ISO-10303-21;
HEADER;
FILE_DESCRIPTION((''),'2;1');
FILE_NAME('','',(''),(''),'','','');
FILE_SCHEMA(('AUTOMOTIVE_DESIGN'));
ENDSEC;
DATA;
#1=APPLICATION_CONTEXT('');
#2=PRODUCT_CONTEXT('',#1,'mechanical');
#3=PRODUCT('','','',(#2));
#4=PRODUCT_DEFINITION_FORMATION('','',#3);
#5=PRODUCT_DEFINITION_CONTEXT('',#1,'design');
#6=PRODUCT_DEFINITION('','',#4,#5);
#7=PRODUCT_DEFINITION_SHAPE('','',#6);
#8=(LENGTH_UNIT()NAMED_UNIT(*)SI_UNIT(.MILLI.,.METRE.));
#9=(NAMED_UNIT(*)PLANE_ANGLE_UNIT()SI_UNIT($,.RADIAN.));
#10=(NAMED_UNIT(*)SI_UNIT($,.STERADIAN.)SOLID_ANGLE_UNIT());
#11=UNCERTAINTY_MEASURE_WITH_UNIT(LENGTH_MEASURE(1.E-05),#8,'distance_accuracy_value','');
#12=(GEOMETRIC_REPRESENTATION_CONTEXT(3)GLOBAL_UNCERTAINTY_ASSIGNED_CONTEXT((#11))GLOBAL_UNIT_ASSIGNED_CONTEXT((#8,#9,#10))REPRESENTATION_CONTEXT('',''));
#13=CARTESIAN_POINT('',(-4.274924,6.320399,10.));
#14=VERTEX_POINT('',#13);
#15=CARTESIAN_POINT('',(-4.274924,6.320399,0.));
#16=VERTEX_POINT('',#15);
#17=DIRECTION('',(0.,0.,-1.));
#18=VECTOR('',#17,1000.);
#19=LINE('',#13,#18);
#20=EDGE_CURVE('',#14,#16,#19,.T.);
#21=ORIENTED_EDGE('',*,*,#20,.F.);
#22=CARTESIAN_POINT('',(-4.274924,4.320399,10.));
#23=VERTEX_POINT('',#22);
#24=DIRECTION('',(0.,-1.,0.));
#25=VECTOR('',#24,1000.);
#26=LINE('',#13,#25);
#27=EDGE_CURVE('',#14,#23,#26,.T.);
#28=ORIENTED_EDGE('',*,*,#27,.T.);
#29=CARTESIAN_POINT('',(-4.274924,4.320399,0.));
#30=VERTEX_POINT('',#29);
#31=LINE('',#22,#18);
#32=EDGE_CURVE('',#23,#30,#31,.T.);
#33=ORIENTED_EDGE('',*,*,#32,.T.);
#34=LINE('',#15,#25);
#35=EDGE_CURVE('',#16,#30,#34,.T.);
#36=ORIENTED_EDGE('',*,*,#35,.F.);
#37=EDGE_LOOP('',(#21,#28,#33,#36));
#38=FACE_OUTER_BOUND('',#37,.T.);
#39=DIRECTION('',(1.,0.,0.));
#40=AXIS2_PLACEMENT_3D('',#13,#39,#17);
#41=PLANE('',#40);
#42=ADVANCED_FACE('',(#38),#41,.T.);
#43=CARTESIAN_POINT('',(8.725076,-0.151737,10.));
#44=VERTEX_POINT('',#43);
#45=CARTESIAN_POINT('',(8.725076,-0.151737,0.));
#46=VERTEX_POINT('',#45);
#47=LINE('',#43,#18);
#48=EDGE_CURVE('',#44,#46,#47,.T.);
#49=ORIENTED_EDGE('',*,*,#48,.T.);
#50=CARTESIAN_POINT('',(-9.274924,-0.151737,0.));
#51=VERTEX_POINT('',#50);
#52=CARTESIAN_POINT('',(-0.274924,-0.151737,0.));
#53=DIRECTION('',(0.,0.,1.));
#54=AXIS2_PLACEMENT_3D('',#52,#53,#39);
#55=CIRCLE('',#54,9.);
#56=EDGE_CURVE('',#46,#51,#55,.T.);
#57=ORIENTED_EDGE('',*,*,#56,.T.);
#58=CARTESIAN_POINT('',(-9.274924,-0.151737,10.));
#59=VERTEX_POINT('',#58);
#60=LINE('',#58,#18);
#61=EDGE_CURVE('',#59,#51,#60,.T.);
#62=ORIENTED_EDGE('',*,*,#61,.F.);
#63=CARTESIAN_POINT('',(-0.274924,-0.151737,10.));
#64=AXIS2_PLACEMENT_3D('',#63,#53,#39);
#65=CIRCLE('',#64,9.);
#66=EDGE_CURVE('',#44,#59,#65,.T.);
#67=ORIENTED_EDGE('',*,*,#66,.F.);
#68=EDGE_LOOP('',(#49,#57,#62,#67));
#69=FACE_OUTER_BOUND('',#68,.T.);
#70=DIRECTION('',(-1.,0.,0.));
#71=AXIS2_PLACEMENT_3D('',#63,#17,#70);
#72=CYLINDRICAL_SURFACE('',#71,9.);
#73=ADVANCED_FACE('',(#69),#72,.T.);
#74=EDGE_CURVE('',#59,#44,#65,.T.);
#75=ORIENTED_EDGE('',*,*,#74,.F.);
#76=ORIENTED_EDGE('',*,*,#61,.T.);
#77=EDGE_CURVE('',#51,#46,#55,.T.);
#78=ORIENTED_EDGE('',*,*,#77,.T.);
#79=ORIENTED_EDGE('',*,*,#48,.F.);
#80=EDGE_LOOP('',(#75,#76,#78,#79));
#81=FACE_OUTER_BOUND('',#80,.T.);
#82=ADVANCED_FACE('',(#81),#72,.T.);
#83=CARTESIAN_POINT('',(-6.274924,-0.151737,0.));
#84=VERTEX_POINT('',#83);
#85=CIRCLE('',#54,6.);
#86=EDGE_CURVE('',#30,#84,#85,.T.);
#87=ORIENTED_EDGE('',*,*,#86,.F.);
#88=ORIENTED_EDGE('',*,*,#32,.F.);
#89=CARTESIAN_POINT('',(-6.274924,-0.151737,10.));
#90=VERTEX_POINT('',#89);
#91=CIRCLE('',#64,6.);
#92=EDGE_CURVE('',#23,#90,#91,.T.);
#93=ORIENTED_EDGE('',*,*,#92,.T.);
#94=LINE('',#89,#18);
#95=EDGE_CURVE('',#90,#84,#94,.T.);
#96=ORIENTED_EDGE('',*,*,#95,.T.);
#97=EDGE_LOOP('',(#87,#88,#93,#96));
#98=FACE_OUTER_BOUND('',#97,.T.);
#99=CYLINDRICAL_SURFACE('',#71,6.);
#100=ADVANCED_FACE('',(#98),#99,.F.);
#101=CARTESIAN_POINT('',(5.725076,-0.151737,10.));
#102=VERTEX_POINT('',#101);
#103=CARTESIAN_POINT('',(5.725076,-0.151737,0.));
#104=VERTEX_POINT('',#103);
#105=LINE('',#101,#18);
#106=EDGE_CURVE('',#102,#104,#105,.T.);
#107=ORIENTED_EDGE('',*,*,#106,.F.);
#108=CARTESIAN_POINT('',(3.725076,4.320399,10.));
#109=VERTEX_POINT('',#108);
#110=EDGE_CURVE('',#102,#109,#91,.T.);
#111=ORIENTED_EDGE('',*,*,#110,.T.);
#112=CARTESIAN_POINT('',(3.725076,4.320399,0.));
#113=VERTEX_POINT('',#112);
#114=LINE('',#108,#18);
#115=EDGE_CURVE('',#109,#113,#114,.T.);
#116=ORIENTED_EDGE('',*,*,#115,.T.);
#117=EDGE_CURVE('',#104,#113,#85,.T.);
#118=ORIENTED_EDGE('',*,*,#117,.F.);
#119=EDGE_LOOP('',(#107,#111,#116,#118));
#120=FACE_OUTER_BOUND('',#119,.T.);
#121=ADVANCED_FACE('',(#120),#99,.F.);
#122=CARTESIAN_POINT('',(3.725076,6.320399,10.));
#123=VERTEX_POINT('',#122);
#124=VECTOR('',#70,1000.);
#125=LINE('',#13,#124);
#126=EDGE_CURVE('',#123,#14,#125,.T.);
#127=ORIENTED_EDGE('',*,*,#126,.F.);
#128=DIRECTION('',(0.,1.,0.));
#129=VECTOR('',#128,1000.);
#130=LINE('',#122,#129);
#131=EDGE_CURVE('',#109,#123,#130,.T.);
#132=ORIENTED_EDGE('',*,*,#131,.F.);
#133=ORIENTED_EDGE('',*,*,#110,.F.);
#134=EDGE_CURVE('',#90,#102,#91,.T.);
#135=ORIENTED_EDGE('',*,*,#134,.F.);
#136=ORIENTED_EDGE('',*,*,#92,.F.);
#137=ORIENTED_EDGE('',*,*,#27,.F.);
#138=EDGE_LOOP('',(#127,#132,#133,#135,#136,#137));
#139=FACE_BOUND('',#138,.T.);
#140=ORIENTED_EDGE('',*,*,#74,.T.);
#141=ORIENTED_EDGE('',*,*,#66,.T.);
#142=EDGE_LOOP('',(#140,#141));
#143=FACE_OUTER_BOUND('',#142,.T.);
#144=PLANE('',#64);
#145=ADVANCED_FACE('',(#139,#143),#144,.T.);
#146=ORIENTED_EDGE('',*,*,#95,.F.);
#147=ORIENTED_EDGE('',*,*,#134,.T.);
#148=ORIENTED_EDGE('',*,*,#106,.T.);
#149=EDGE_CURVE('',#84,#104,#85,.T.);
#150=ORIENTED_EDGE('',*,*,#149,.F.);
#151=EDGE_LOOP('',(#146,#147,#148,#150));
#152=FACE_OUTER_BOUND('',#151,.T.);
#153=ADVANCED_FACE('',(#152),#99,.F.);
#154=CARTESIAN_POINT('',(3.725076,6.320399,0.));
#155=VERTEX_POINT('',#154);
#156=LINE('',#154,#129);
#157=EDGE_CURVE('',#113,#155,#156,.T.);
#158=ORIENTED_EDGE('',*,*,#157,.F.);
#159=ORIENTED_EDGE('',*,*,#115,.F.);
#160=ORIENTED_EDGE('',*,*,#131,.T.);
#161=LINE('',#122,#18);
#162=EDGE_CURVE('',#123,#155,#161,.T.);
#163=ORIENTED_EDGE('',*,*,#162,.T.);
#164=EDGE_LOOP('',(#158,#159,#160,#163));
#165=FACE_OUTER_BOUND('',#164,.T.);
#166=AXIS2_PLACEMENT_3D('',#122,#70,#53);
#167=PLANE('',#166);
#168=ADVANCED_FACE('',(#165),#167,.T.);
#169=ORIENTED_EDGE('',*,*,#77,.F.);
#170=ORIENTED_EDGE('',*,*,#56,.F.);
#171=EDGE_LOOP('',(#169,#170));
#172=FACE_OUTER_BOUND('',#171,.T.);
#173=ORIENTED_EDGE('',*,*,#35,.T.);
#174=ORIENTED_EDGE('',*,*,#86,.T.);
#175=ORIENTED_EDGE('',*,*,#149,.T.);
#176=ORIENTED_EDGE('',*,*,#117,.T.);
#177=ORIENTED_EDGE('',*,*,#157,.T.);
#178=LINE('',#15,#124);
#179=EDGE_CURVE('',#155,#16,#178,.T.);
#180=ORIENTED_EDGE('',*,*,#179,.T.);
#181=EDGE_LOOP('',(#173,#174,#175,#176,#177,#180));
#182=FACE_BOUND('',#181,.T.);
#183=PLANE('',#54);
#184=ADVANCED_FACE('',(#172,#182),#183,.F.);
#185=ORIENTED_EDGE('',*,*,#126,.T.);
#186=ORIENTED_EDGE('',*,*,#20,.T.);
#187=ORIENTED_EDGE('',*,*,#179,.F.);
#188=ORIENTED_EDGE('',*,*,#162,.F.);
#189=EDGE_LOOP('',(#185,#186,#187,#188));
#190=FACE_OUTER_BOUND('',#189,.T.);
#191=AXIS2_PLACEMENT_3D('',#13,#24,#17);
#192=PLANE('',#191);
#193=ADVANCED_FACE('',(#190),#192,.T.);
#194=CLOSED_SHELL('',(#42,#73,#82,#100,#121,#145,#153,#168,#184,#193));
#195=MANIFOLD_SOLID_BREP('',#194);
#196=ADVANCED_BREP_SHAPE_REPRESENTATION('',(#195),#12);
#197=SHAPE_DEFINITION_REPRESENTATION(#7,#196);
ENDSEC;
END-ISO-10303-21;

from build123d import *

# Parameters (mm, degrees)
SKETCH_1_R      = 9
EXTRUDE_1_DEPTH = 10


with BuildPart() as part:
    # 草图1 → 凸台-拉伸1 (new body)
    with BuildSketch(Plane.XY):
        with Locations((-0.274924045, -0.151737187)):
            Circle(SKETCH_1_R)
        with BuildLine():
            Line((-4.274924045, 6.320398768), (3.725075955, 6.320398768))
            Line((3.725075955, 6.320398768), (3.725075955, 4.320398768))
            ThreePointArc((3.725075955, 4.320398768), (-0.274924045, -6.151737187), (-4.274924045, 4.320398768))
            Line((-4.274924045, 4.320398768), (-4.274924045, 6.320398768))
        make_face(mode=Mode.SUBTRACT)
    extrude(amount=EXTRUDE_1_DEPTH)


solid = part.part
